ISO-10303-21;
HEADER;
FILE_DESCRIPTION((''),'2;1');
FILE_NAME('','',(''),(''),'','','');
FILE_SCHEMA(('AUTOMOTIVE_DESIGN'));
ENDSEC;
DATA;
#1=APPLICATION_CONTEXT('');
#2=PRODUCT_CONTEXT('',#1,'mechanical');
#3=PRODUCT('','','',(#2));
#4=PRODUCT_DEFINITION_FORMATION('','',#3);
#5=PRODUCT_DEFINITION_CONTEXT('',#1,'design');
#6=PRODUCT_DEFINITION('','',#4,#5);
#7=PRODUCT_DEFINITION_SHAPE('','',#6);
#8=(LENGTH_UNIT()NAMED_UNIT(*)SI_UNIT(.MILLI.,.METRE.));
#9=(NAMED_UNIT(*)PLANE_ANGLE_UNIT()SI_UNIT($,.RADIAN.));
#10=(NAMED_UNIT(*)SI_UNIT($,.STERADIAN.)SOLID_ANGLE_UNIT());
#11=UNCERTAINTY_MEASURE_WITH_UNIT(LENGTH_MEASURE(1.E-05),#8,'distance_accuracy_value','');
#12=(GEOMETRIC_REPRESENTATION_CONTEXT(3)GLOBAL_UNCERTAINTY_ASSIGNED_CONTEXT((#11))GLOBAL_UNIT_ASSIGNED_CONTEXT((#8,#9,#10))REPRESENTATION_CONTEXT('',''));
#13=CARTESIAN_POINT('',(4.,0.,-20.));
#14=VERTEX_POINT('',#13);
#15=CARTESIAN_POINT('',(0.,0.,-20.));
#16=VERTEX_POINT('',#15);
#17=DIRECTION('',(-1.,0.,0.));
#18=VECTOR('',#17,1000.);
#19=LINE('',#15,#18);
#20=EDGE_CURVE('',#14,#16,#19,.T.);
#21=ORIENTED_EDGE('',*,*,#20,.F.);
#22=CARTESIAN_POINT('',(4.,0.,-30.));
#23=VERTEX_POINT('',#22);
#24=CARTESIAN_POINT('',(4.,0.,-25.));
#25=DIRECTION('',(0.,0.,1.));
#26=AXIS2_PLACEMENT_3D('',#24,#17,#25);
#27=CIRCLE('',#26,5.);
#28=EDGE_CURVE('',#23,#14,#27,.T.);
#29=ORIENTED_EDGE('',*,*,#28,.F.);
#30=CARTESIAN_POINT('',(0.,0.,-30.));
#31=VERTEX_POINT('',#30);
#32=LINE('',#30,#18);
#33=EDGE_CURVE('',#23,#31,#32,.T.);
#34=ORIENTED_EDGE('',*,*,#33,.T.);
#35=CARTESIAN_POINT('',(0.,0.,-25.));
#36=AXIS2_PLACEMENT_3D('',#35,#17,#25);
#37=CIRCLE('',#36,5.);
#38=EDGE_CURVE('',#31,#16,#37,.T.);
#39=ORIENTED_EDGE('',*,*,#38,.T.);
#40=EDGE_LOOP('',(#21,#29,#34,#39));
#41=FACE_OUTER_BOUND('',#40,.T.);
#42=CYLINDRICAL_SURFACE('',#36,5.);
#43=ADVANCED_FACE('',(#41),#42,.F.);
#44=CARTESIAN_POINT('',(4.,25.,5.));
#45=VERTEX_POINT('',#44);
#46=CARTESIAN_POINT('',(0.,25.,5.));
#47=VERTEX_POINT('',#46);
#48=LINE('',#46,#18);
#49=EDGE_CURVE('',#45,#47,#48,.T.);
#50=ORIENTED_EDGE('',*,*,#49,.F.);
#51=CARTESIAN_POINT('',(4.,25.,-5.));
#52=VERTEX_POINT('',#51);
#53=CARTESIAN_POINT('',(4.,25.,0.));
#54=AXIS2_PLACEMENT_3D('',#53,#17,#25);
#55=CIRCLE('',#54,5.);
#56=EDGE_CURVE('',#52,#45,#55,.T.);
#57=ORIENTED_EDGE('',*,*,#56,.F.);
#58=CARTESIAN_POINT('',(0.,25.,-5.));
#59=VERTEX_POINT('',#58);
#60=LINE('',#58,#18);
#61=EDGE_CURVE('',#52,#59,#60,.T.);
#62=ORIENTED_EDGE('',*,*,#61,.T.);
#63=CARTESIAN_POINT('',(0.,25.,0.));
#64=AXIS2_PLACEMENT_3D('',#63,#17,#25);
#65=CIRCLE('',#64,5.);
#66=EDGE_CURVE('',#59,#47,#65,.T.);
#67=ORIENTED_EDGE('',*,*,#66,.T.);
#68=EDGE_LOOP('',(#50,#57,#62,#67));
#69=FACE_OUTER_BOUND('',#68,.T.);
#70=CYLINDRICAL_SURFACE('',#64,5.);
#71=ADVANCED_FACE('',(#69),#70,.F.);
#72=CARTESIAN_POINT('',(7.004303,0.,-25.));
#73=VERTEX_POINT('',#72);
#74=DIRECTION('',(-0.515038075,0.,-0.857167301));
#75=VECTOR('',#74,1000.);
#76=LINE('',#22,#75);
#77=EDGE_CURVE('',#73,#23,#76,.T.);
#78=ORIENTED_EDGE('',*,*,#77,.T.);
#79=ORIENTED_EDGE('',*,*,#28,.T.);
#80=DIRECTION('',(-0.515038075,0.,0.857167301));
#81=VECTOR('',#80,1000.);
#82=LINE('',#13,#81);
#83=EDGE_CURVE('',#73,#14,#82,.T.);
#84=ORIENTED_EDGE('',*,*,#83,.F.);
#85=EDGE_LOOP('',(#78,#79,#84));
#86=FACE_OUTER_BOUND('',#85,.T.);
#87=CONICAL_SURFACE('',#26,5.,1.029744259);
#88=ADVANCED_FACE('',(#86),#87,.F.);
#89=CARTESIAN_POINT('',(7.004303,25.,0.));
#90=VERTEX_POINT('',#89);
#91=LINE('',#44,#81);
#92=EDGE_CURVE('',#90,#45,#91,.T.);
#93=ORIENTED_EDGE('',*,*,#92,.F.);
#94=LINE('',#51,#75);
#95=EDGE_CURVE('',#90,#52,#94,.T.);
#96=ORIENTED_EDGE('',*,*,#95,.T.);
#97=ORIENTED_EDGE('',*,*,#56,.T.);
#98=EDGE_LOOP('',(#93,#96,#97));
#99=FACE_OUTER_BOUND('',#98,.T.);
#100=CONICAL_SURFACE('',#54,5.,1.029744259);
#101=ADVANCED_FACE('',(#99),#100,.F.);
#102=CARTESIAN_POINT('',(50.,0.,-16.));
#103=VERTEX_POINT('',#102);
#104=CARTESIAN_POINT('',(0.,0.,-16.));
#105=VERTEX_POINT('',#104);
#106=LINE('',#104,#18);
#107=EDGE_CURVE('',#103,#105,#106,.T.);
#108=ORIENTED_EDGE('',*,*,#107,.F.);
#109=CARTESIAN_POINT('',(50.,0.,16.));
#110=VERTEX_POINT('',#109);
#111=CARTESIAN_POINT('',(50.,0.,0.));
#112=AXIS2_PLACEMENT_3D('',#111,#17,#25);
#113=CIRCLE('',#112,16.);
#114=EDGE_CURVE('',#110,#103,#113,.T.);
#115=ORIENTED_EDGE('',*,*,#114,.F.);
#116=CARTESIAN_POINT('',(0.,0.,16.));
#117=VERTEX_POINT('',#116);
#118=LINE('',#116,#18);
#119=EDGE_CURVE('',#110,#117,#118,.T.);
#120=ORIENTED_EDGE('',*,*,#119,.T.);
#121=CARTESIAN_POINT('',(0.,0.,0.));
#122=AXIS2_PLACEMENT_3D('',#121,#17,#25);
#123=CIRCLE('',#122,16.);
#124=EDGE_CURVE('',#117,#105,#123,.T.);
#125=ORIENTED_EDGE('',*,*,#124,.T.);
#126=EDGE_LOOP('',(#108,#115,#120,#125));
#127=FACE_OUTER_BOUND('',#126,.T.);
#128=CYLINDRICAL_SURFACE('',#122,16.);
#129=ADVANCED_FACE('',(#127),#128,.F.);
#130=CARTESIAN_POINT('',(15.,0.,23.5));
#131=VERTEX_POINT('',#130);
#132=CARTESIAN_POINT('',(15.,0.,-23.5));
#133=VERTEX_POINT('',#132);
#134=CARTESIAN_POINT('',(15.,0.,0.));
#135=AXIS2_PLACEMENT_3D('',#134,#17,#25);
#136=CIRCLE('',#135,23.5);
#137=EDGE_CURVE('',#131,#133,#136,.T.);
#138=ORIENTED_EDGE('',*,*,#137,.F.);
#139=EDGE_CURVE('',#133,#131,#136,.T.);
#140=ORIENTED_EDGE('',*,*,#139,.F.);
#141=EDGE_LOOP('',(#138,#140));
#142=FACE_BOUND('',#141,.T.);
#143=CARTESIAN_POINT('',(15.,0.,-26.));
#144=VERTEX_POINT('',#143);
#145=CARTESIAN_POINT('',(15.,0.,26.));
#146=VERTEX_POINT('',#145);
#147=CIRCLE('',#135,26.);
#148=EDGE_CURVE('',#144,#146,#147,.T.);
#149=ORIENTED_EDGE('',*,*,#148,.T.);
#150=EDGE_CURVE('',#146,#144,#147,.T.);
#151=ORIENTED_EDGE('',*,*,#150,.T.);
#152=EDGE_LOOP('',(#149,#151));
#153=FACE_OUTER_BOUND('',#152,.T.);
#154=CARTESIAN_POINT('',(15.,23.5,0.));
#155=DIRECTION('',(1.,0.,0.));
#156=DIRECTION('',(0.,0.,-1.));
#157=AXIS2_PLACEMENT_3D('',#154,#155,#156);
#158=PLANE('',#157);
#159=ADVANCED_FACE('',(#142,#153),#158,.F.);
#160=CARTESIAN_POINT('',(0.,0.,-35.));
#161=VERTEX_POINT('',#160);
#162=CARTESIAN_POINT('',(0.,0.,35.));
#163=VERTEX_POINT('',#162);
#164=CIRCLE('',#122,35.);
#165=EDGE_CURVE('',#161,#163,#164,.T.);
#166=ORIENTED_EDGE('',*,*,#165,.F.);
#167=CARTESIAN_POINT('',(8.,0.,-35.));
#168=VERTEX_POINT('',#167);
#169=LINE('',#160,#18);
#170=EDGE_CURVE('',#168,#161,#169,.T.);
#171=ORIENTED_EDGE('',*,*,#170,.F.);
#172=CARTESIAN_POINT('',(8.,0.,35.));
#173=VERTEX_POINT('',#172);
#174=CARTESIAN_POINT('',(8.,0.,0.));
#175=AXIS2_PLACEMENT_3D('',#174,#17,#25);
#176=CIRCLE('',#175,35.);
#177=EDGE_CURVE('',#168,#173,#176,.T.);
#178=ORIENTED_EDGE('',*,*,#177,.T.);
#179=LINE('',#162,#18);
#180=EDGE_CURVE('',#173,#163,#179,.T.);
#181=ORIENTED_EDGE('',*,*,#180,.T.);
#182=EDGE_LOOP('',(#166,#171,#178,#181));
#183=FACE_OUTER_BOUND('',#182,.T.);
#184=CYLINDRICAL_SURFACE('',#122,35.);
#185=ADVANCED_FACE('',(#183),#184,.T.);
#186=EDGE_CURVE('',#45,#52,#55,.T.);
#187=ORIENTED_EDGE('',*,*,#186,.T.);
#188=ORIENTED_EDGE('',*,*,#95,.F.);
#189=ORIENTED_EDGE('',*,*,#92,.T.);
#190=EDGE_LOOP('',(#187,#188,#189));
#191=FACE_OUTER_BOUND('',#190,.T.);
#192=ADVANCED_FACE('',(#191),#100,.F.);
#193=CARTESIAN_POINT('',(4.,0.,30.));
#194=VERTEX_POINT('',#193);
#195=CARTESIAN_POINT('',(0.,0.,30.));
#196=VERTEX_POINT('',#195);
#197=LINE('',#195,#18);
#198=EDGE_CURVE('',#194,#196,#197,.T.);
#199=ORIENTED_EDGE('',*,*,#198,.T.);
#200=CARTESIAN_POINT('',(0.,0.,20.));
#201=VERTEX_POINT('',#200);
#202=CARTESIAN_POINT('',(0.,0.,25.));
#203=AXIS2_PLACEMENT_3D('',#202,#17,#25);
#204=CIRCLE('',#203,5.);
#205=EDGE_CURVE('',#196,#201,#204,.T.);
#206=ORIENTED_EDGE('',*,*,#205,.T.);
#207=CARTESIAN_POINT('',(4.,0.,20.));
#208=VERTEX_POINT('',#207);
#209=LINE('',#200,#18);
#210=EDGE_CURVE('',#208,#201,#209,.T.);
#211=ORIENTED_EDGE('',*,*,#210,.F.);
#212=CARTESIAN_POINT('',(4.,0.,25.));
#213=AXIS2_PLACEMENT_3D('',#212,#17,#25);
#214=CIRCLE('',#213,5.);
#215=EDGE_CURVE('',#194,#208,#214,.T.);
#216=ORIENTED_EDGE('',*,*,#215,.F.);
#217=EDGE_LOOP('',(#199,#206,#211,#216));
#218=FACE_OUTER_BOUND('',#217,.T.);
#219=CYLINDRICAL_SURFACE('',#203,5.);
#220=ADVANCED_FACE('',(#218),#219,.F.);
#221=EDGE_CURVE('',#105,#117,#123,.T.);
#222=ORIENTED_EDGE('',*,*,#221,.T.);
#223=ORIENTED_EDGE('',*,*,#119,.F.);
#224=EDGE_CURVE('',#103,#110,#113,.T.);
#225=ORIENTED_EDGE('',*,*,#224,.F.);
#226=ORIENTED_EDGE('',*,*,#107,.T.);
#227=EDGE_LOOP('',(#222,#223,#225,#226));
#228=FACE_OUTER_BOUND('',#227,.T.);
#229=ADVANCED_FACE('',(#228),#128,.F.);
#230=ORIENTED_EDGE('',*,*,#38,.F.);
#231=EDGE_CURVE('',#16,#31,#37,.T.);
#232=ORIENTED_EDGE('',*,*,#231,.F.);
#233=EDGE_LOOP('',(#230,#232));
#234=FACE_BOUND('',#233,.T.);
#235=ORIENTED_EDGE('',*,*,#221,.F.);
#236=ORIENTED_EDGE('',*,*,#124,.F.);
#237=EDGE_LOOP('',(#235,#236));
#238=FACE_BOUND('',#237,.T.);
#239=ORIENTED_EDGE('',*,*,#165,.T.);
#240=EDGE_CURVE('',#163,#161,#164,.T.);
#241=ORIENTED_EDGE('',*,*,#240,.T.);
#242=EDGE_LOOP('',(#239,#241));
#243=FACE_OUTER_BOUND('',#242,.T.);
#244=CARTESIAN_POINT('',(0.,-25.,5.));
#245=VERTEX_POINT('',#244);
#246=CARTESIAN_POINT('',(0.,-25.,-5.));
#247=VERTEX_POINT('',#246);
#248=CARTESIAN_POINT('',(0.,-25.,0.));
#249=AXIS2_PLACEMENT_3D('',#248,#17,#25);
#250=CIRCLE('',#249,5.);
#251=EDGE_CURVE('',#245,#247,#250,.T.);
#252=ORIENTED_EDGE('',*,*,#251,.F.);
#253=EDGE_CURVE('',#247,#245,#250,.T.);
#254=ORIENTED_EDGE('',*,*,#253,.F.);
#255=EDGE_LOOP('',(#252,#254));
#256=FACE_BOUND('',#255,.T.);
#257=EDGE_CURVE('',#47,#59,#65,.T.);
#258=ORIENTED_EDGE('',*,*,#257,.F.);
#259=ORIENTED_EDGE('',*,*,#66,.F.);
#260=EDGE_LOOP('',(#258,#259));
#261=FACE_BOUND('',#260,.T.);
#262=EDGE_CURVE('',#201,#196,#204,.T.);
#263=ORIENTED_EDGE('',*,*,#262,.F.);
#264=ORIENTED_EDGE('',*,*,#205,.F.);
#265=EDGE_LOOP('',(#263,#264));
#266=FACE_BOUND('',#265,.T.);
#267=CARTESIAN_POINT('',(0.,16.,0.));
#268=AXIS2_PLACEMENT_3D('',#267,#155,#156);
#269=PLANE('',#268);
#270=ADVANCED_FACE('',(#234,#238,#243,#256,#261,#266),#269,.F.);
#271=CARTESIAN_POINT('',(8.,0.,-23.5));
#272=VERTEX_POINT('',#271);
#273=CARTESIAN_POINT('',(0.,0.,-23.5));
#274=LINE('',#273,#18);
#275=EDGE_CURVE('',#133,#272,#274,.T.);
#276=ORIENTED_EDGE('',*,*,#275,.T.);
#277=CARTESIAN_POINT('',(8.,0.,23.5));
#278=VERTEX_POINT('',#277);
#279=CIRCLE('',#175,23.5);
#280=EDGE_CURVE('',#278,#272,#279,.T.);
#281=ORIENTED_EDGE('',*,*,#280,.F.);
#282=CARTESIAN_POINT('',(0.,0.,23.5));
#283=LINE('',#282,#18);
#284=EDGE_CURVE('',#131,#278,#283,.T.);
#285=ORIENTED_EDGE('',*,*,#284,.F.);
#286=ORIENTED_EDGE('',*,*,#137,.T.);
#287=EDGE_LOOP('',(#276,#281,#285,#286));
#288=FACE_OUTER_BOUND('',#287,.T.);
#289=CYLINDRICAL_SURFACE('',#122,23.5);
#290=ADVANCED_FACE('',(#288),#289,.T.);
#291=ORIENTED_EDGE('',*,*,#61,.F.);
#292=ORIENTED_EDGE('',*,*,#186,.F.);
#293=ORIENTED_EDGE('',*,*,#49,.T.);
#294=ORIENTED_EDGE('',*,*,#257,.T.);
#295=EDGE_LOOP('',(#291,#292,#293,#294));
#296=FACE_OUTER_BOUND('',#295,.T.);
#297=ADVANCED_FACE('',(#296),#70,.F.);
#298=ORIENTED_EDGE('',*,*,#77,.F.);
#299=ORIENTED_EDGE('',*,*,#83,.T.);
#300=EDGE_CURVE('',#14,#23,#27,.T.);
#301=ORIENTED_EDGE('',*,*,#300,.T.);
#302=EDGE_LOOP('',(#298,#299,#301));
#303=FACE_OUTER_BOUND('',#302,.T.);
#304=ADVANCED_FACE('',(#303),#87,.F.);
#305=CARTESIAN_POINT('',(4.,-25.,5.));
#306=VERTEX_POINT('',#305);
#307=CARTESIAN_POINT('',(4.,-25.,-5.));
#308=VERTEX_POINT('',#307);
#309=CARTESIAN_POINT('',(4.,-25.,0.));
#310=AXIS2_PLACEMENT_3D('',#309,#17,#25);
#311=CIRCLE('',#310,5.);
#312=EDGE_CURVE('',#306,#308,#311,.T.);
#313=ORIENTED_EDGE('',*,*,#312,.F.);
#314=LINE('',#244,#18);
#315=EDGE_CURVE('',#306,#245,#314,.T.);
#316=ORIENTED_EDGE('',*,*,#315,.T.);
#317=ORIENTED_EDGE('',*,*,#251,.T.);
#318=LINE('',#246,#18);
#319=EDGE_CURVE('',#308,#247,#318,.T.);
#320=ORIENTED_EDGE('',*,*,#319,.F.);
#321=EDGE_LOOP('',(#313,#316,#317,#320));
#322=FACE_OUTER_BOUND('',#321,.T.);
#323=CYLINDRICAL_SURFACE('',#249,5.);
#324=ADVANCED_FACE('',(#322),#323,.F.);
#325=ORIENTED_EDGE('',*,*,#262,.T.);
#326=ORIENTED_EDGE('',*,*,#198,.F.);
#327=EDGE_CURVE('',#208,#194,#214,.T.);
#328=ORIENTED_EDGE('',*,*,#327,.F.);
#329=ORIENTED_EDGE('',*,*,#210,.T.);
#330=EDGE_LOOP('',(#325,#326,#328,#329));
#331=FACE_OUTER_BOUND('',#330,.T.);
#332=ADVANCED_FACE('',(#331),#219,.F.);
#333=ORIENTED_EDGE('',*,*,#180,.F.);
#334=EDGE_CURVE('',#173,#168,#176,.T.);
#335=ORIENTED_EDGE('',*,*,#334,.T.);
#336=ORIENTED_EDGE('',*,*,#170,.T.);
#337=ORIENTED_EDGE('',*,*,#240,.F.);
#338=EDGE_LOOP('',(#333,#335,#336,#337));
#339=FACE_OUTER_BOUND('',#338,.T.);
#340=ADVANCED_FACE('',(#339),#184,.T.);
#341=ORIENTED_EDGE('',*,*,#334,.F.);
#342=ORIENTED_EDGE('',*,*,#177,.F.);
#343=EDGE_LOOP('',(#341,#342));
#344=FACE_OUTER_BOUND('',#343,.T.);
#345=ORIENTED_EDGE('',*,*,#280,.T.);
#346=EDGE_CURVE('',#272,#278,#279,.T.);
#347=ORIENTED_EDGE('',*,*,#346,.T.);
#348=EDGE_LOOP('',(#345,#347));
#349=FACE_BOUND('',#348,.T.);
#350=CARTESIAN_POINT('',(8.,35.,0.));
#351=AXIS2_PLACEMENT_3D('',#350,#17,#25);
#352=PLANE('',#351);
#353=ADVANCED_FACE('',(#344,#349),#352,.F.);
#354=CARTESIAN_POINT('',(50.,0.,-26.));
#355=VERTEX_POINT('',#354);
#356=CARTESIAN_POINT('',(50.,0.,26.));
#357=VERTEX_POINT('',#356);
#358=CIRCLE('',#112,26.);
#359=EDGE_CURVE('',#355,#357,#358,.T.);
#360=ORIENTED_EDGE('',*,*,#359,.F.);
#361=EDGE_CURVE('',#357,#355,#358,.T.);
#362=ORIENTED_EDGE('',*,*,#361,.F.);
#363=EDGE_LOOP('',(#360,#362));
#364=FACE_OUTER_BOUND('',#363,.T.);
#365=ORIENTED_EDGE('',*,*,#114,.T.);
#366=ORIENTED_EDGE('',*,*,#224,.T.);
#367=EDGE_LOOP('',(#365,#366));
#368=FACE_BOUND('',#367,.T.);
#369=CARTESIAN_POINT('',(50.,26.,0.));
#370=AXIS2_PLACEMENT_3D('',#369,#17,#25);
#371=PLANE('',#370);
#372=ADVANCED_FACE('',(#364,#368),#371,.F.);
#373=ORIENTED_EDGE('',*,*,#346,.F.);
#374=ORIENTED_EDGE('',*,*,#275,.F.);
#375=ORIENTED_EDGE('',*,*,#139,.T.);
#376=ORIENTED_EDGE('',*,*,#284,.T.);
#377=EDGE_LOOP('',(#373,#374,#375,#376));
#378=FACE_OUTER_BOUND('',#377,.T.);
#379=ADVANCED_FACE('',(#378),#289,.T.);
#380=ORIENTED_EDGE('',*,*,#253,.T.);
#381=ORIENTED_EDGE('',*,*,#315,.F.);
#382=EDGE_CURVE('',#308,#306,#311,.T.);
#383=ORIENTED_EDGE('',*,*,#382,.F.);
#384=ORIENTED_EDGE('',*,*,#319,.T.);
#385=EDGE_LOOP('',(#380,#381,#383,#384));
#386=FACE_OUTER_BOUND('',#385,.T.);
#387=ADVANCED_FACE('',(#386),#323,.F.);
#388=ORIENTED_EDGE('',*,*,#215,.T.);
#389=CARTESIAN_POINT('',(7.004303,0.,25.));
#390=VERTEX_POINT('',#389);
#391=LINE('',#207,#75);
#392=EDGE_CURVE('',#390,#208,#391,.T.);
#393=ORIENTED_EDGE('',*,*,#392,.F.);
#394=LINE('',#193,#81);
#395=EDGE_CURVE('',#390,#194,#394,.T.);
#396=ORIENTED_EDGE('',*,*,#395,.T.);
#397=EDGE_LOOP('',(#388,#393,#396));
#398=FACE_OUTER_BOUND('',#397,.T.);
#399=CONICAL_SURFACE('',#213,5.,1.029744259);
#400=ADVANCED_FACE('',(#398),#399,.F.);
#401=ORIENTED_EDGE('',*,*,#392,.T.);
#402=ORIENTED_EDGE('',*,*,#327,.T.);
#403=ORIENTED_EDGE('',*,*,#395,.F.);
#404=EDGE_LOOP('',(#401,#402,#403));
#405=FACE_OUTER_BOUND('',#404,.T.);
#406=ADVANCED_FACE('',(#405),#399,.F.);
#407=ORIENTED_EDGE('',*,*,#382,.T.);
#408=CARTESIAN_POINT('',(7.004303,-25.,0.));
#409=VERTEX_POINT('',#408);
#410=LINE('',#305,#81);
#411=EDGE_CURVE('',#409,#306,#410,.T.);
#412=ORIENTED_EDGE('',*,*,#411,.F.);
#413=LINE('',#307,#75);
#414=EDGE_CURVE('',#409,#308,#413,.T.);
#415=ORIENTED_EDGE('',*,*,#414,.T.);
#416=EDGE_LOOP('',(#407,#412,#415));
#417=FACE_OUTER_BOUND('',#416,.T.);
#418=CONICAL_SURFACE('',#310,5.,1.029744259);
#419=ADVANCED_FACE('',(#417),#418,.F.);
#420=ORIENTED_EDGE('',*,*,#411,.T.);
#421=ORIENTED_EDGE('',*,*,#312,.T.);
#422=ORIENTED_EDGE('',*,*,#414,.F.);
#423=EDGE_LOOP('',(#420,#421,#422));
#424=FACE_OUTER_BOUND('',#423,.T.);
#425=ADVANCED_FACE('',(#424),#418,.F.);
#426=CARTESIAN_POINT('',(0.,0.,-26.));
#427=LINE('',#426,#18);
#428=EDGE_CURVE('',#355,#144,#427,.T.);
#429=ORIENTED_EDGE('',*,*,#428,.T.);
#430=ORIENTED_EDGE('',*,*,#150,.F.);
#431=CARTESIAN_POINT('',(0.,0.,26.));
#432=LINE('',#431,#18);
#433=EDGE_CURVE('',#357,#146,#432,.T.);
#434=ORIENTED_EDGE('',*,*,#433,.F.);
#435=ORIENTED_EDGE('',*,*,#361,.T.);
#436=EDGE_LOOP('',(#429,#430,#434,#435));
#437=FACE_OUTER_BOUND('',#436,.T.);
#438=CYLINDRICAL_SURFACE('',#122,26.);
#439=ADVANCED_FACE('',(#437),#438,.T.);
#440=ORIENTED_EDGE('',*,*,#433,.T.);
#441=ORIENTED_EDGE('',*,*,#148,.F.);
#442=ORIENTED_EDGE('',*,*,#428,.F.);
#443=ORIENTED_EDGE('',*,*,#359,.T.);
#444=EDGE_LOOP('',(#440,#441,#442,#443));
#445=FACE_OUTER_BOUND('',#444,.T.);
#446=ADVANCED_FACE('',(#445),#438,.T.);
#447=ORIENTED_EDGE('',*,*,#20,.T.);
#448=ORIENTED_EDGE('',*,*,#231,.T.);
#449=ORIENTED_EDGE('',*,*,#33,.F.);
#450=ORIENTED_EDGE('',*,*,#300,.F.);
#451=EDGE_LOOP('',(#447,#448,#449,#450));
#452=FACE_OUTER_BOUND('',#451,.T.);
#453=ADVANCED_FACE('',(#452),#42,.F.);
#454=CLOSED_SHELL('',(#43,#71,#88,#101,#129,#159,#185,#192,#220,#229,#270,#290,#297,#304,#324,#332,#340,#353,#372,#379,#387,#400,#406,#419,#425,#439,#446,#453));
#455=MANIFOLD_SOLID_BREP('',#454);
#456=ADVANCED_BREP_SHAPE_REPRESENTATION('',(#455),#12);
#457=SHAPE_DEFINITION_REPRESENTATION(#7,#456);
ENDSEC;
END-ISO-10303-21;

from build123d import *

# Parameters (mm, degrees)
CIRPATTERN1_COUNT = 4


with BuildPart() as part:
    # Sketch1 → Revolve1 (revolve)
    with BuildSketch(Plane.XY, mode=Mode.PRIVATE) as revolve1_sk:
        Polygon((0, 16), (0, 35), (8, 35), (8, 23.5), (15, 23.5), (15, 26), (50, 26), (50, 16), align=None)
    revolve(revolve1_sk.sketch.rotate(Axis((0, 0, 0), (1, 0, 0)), 90), axis=Axis((0, 0, 0), (1, 0, 0)))

    # Sketch3 → Ø10.0 (10) Diameter Hole1 (revolve, cut)
    with BuildSketch(Plane.ZX.offset(25)):
        Polygon((0, 0), (0, 7.004303095), (5, 4), (5, 0), align=None)
    f_10_0_10_diameter_hole1 = revolve(axis=Axis((-6.35, 25, 0), (1, 0, 0)), mode=Mode.SUBTRACT)

    # CirPattern1: Ø10.0 (10) Diameter Hole1 ×4 about axis
    cirpattern1_axis = Axis((0, 0, 0), (1, 0, 0))
    for i in range(1, CIRPATTERN1_COUNT):
        add(f_10_0_10_diameter_hole1.rotate(cirpattern1_axis, i * 360 / CIRPATTERN1_COUNT), mode=Mode.SUBTRACT)


solid = part.part
